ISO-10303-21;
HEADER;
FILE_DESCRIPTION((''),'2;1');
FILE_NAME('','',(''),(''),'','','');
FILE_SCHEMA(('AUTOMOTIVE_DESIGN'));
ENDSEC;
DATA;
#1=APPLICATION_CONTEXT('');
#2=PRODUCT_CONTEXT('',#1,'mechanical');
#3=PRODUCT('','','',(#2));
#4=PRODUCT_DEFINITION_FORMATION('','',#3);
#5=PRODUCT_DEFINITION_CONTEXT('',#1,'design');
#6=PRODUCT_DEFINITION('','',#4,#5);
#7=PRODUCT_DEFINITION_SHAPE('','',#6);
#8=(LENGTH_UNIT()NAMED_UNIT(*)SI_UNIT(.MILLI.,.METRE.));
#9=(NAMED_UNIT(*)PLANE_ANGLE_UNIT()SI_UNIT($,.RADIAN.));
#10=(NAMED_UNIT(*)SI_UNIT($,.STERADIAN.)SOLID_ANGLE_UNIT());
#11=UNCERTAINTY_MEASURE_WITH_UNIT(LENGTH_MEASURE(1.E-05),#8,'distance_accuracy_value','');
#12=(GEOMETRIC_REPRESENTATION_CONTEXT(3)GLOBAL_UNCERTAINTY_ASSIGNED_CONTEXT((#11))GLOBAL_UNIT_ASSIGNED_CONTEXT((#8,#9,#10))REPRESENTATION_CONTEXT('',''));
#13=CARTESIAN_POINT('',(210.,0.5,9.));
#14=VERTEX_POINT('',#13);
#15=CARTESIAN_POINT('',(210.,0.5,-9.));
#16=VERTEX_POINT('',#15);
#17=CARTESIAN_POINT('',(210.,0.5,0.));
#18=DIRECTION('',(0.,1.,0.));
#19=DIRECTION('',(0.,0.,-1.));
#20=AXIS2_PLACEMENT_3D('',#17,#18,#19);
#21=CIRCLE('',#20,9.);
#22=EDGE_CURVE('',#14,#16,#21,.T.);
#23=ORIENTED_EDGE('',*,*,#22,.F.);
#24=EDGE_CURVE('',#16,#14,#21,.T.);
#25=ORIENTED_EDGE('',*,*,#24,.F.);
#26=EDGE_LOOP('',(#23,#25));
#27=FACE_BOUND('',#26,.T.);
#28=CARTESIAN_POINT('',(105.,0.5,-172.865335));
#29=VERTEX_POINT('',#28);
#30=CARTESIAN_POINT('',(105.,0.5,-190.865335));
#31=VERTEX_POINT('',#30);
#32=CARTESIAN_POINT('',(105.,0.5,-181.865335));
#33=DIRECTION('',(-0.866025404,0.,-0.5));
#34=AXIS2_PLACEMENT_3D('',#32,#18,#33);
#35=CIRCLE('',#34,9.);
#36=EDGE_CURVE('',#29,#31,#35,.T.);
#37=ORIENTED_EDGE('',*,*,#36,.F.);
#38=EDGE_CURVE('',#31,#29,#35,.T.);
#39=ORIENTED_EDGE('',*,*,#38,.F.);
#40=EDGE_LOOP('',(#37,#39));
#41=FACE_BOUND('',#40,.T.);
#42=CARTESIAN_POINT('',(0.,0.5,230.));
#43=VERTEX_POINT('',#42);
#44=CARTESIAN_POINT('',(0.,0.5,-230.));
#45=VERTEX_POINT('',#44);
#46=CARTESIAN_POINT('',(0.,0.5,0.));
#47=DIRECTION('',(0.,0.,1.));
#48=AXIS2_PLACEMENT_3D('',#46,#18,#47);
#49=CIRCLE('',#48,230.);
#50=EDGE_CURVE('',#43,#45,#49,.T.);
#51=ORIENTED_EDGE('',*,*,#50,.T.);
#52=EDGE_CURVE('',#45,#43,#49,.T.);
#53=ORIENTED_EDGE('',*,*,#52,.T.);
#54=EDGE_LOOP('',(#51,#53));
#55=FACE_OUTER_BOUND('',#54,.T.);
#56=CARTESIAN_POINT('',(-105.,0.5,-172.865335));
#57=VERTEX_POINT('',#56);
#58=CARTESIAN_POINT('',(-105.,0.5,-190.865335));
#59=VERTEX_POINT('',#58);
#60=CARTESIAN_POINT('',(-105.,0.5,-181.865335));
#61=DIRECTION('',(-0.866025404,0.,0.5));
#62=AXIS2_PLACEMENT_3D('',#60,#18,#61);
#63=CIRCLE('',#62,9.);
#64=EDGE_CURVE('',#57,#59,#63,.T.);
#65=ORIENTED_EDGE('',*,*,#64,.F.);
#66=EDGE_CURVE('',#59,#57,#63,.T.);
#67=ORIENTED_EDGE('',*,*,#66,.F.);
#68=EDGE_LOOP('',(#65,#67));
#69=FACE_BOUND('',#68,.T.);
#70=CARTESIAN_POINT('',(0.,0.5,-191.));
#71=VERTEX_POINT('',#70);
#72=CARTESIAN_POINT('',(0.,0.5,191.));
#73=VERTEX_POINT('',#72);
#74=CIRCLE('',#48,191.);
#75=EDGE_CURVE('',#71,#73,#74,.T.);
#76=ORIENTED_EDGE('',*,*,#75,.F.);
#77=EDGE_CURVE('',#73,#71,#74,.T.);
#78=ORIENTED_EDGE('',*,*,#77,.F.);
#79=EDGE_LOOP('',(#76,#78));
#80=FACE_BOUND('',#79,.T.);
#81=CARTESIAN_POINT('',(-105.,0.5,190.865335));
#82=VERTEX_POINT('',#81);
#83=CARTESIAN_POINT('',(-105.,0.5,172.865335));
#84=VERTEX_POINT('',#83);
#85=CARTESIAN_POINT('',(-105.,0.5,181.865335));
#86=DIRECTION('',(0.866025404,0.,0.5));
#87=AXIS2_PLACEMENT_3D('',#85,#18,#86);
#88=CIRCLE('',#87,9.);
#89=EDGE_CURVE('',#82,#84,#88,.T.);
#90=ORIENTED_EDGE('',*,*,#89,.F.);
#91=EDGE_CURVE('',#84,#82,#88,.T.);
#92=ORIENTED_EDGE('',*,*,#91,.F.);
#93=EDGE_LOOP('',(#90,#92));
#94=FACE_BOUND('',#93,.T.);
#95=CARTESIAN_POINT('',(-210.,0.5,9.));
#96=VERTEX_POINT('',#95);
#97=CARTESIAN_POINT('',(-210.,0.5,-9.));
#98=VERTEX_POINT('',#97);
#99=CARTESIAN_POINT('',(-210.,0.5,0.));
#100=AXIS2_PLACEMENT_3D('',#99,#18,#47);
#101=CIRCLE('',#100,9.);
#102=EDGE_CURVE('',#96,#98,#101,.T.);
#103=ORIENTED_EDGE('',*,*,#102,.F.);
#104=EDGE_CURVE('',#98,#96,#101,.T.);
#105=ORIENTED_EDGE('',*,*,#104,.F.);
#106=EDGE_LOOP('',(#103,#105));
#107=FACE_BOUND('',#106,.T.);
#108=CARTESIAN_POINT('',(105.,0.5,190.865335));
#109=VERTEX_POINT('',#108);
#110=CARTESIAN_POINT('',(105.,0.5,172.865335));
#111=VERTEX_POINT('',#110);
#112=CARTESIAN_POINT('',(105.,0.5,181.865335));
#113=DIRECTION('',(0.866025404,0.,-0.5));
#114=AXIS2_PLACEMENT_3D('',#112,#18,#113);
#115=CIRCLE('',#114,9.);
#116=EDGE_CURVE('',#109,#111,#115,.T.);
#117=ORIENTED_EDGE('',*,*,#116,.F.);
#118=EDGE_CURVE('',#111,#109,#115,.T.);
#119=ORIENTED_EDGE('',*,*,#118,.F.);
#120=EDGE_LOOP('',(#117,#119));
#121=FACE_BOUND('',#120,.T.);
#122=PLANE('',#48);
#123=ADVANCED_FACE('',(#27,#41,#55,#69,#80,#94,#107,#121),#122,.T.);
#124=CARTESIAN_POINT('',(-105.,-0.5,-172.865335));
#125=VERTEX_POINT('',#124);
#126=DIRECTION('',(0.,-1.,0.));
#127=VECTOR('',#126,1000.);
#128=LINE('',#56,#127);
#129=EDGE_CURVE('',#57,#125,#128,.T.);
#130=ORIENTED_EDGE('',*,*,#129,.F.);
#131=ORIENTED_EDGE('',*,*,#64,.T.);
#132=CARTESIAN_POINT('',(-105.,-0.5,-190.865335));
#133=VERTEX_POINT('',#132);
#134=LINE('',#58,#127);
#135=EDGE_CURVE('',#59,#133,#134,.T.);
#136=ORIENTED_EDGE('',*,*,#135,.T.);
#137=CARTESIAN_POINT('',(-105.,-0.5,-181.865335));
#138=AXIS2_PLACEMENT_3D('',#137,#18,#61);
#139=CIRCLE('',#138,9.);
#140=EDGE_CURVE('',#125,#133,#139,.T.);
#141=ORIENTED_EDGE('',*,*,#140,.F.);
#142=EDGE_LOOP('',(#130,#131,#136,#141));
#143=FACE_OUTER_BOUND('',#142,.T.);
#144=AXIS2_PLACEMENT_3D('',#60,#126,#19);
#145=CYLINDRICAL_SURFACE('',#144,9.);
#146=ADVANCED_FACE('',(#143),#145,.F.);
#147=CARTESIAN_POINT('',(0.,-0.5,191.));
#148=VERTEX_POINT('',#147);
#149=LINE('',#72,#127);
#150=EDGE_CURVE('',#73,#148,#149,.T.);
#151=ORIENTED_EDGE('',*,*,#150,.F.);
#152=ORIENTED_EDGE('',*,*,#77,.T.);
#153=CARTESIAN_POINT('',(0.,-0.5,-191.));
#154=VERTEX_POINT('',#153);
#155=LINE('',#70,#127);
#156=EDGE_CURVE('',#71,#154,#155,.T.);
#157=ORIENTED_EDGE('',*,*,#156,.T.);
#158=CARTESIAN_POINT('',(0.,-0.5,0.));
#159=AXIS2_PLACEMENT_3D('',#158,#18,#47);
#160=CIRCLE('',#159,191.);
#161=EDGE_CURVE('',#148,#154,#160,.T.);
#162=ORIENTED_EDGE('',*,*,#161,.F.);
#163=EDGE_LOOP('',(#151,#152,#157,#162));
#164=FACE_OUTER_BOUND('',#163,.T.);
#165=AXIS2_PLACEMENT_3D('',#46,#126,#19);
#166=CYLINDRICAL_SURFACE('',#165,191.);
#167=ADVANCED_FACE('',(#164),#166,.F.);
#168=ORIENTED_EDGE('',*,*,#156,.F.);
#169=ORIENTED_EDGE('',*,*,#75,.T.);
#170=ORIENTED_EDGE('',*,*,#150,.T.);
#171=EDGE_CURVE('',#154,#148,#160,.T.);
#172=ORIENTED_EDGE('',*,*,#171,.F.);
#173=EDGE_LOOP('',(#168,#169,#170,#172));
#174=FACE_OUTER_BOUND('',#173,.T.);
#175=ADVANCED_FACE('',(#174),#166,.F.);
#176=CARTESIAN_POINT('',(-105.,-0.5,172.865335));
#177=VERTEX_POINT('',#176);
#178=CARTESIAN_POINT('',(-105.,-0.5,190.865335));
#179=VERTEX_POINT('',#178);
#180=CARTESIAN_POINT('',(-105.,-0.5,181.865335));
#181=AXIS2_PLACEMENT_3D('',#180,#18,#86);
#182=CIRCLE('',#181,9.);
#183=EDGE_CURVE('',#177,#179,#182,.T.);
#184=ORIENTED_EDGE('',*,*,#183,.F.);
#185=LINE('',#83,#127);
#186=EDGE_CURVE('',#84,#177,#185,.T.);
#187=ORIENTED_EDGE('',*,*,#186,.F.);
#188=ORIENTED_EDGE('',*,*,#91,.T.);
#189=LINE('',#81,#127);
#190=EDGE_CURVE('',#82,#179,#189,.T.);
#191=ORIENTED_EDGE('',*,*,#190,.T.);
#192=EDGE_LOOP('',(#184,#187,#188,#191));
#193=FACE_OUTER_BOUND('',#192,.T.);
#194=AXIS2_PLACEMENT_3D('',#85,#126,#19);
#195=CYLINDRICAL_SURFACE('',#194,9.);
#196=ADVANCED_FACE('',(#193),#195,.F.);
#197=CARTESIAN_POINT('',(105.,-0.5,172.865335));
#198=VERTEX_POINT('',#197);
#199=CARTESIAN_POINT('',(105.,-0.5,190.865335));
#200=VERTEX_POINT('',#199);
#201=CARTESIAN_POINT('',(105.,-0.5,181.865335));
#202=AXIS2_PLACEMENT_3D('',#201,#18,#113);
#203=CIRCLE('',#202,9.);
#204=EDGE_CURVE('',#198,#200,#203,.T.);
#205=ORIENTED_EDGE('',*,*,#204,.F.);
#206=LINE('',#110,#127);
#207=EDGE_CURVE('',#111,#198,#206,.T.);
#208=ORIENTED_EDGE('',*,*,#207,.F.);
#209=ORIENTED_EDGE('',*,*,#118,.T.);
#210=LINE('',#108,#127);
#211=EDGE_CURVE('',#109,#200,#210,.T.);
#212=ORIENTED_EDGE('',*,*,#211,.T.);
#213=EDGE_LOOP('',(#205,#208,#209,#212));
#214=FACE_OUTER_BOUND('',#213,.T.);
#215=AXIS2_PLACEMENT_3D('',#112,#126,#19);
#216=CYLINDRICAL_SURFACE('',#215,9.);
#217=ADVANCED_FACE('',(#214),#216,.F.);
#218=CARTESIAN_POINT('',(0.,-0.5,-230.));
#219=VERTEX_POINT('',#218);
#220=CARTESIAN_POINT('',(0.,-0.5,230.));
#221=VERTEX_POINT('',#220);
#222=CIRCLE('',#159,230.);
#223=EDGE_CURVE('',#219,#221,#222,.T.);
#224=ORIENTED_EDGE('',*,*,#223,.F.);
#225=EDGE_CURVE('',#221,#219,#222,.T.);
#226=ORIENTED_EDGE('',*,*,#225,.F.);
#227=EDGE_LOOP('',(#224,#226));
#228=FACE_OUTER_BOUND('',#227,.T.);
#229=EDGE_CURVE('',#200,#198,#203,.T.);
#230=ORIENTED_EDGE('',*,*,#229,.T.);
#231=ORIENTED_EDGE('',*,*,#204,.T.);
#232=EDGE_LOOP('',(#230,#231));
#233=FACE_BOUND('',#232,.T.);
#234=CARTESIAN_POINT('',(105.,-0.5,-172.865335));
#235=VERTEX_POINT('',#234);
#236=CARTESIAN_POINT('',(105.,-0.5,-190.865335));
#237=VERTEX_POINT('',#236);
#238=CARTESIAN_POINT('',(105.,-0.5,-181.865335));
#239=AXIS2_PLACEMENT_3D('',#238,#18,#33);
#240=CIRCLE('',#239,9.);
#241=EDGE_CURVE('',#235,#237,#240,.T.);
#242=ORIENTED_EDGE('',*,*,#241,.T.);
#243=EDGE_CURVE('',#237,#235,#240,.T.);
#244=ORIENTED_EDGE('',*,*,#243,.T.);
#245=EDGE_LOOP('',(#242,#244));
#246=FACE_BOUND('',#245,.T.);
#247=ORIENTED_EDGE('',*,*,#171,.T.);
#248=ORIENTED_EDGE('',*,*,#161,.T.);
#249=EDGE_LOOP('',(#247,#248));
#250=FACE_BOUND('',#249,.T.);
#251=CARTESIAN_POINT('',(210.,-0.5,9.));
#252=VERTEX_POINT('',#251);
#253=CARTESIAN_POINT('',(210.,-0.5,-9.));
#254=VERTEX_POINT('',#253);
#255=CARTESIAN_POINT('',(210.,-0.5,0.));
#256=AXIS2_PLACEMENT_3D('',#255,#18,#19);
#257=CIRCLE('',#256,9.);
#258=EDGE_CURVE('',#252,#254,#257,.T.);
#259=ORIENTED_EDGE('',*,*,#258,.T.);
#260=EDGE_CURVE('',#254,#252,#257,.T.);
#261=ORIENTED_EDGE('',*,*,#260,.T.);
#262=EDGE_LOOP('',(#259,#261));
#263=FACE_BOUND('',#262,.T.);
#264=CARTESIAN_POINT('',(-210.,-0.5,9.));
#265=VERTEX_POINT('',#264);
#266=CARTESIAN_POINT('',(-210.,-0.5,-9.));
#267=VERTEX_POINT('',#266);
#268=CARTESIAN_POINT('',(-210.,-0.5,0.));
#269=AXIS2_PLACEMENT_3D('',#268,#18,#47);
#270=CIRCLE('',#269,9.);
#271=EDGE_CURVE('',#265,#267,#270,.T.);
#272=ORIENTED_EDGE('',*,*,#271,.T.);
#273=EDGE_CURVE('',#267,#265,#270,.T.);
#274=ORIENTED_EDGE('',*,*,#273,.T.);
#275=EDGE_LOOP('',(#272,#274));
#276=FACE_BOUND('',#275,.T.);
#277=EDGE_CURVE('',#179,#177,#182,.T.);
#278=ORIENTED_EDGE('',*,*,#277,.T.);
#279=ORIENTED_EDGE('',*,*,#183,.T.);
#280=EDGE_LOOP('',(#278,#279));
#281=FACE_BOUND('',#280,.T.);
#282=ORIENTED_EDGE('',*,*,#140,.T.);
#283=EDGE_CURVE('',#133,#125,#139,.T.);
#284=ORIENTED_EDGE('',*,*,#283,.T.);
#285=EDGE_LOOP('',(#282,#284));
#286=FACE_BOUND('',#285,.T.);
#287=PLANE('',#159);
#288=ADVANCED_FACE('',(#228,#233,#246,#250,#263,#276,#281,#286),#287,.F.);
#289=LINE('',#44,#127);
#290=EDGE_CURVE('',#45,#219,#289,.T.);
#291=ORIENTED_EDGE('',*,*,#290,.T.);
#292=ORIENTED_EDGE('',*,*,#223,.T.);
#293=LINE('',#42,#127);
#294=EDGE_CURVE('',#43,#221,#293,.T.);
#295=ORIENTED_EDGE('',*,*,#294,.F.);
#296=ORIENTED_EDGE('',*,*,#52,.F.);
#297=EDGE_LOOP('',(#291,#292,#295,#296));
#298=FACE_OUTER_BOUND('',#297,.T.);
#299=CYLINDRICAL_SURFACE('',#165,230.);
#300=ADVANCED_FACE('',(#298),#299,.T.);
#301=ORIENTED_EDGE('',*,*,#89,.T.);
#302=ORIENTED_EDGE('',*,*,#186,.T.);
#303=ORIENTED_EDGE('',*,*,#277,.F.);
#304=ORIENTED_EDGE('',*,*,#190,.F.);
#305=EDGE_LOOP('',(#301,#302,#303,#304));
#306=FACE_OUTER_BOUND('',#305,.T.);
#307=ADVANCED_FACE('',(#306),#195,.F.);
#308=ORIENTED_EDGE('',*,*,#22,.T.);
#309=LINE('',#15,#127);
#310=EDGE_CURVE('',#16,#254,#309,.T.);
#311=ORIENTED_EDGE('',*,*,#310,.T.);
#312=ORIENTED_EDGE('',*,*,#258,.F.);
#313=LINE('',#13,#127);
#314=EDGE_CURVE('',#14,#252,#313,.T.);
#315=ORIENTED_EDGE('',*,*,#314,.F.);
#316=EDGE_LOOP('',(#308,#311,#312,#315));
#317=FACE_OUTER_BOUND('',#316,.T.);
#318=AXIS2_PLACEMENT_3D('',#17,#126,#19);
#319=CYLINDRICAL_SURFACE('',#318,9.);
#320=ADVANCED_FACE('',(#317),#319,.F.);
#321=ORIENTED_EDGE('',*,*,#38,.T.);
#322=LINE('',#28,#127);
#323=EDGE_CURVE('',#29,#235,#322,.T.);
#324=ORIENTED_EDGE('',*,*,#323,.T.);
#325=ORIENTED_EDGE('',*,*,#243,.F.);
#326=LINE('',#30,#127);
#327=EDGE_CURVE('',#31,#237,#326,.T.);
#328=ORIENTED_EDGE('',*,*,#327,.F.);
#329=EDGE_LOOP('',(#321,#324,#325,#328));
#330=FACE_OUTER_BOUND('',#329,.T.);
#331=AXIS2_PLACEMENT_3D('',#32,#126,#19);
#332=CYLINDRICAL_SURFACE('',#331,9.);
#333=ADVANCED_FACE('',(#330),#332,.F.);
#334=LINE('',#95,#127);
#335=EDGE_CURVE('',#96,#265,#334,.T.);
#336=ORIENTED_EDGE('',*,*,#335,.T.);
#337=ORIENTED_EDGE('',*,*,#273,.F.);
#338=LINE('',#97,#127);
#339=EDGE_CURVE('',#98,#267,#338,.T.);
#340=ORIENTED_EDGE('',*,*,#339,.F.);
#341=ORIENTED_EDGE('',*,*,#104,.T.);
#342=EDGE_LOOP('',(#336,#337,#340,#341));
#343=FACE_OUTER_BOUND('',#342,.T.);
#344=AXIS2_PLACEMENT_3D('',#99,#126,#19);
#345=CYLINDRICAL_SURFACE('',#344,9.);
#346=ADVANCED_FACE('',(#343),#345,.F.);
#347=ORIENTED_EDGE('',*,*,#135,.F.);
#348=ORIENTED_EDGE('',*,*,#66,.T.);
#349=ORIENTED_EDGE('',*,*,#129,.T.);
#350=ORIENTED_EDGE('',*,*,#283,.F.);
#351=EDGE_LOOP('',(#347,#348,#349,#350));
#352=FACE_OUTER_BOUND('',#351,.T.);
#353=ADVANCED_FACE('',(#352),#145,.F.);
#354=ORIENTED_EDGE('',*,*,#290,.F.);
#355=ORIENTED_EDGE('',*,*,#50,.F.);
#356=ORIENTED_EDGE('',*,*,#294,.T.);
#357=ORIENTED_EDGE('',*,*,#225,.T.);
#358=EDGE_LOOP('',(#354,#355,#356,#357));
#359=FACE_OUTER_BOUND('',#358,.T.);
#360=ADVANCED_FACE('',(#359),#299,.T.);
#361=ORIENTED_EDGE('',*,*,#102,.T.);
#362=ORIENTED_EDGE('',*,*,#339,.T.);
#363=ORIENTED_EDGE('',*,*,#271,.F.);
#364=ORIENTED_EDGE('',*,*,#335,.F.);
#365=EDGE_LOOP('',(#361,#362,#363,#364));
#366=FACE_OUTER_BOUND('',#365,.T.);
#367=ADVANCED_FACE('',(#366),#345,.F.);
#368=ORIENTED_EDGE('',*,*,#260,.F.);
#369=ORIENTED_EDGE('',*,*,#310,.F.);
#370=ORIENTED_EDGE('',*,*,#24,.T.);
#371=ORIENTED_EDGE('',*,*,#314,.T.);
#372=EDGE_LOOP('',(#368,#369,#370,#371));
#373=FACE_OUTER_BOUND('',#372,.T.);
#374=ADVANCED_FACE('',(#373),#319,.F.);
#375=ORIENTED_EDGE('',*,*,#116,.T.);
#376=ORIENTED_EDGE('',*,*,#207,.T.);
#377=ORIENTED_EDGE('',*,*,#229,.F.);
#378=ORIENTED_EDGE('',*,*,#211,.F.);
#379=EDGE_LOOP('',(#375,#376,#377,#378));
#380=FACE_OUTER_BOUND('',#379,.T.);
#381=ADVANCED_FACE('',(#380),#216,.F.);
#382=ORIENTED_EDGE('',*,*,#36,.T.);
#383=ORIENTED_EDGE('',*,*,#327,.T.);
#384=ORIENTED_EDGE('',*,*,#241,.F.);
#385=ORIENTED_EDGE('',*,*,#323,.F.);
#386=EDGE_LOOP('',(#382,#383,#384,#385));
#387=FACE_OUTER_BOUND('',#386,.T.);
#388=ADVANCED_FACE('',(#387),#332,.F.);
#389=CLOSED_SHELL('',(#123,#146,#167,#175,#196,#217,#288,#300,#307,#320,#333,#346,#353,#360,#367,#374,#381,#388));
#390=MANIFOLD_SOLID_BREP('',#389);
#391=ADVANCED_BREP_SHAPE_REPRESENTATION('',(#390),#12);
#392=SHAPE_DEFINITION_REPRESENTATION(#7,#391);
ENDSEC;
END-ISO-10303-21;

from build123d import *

# Parameters (mm, degrees)
SKETCH1_R           = 230
SKETCH1_R_2         = 191
BOSS_EXTRUDE1_DEPTH = 0.5
SKETCH2_R           = 9
CUT_EXTRUDE2_DEPTH  = 0.5
CIRPATTERN1_COUNT   = 6


with BuildPart() as part:
    # Sketch1 → Boss-Extrude1 (new, symmetric)
    with BuildSketch(Plane(origin=(0, 0, 0), x_dir=(1, 0, 0), z_dir=(0, 1, 0))):
        with Locations(Location((0, 0, 0), (0, 0, 270))):
            Circle(SKETCH1_R)
        with Locations(Location((0, 0, 0), (0, 0, 270))):
            Circle(SKETCH1_R_2, mode=Mode.SUBTRACT)
    extrude(amount=BOSS_EXTRUDE1_DEPTH, both=True)

    # Sketch2 → Cut-Extrude2 (cut, symmetric)
    with BuildSketch(Plane(origin=(0, 0, 0), x_dir=(1, 0, 0), z_dir=(0, 1, 0))):
        with Locations(Location((-210, 0, 0), (0, 0, 270))):
            Circle(SKETCH2_R)
    cut_extrude2 = extrude(amount=CUT_EXTRUDE2_DEPTH, both=True, mode=Mode.SUBTRACT)

    # CirPattern1: Cut-Extrude2 ×6 about axis
    cirpattern1_axis = Axis((0, 0, 0), (0, 1, 0))
    for i in range(1, CIRPATTERN1_COUNT):
        add(cut_extrude2.rotate(cirpattern1_axis, i * 360 / CIRPATTERN1_COUNT), mode=Mode.SUBTRACT)


solid = part.part
